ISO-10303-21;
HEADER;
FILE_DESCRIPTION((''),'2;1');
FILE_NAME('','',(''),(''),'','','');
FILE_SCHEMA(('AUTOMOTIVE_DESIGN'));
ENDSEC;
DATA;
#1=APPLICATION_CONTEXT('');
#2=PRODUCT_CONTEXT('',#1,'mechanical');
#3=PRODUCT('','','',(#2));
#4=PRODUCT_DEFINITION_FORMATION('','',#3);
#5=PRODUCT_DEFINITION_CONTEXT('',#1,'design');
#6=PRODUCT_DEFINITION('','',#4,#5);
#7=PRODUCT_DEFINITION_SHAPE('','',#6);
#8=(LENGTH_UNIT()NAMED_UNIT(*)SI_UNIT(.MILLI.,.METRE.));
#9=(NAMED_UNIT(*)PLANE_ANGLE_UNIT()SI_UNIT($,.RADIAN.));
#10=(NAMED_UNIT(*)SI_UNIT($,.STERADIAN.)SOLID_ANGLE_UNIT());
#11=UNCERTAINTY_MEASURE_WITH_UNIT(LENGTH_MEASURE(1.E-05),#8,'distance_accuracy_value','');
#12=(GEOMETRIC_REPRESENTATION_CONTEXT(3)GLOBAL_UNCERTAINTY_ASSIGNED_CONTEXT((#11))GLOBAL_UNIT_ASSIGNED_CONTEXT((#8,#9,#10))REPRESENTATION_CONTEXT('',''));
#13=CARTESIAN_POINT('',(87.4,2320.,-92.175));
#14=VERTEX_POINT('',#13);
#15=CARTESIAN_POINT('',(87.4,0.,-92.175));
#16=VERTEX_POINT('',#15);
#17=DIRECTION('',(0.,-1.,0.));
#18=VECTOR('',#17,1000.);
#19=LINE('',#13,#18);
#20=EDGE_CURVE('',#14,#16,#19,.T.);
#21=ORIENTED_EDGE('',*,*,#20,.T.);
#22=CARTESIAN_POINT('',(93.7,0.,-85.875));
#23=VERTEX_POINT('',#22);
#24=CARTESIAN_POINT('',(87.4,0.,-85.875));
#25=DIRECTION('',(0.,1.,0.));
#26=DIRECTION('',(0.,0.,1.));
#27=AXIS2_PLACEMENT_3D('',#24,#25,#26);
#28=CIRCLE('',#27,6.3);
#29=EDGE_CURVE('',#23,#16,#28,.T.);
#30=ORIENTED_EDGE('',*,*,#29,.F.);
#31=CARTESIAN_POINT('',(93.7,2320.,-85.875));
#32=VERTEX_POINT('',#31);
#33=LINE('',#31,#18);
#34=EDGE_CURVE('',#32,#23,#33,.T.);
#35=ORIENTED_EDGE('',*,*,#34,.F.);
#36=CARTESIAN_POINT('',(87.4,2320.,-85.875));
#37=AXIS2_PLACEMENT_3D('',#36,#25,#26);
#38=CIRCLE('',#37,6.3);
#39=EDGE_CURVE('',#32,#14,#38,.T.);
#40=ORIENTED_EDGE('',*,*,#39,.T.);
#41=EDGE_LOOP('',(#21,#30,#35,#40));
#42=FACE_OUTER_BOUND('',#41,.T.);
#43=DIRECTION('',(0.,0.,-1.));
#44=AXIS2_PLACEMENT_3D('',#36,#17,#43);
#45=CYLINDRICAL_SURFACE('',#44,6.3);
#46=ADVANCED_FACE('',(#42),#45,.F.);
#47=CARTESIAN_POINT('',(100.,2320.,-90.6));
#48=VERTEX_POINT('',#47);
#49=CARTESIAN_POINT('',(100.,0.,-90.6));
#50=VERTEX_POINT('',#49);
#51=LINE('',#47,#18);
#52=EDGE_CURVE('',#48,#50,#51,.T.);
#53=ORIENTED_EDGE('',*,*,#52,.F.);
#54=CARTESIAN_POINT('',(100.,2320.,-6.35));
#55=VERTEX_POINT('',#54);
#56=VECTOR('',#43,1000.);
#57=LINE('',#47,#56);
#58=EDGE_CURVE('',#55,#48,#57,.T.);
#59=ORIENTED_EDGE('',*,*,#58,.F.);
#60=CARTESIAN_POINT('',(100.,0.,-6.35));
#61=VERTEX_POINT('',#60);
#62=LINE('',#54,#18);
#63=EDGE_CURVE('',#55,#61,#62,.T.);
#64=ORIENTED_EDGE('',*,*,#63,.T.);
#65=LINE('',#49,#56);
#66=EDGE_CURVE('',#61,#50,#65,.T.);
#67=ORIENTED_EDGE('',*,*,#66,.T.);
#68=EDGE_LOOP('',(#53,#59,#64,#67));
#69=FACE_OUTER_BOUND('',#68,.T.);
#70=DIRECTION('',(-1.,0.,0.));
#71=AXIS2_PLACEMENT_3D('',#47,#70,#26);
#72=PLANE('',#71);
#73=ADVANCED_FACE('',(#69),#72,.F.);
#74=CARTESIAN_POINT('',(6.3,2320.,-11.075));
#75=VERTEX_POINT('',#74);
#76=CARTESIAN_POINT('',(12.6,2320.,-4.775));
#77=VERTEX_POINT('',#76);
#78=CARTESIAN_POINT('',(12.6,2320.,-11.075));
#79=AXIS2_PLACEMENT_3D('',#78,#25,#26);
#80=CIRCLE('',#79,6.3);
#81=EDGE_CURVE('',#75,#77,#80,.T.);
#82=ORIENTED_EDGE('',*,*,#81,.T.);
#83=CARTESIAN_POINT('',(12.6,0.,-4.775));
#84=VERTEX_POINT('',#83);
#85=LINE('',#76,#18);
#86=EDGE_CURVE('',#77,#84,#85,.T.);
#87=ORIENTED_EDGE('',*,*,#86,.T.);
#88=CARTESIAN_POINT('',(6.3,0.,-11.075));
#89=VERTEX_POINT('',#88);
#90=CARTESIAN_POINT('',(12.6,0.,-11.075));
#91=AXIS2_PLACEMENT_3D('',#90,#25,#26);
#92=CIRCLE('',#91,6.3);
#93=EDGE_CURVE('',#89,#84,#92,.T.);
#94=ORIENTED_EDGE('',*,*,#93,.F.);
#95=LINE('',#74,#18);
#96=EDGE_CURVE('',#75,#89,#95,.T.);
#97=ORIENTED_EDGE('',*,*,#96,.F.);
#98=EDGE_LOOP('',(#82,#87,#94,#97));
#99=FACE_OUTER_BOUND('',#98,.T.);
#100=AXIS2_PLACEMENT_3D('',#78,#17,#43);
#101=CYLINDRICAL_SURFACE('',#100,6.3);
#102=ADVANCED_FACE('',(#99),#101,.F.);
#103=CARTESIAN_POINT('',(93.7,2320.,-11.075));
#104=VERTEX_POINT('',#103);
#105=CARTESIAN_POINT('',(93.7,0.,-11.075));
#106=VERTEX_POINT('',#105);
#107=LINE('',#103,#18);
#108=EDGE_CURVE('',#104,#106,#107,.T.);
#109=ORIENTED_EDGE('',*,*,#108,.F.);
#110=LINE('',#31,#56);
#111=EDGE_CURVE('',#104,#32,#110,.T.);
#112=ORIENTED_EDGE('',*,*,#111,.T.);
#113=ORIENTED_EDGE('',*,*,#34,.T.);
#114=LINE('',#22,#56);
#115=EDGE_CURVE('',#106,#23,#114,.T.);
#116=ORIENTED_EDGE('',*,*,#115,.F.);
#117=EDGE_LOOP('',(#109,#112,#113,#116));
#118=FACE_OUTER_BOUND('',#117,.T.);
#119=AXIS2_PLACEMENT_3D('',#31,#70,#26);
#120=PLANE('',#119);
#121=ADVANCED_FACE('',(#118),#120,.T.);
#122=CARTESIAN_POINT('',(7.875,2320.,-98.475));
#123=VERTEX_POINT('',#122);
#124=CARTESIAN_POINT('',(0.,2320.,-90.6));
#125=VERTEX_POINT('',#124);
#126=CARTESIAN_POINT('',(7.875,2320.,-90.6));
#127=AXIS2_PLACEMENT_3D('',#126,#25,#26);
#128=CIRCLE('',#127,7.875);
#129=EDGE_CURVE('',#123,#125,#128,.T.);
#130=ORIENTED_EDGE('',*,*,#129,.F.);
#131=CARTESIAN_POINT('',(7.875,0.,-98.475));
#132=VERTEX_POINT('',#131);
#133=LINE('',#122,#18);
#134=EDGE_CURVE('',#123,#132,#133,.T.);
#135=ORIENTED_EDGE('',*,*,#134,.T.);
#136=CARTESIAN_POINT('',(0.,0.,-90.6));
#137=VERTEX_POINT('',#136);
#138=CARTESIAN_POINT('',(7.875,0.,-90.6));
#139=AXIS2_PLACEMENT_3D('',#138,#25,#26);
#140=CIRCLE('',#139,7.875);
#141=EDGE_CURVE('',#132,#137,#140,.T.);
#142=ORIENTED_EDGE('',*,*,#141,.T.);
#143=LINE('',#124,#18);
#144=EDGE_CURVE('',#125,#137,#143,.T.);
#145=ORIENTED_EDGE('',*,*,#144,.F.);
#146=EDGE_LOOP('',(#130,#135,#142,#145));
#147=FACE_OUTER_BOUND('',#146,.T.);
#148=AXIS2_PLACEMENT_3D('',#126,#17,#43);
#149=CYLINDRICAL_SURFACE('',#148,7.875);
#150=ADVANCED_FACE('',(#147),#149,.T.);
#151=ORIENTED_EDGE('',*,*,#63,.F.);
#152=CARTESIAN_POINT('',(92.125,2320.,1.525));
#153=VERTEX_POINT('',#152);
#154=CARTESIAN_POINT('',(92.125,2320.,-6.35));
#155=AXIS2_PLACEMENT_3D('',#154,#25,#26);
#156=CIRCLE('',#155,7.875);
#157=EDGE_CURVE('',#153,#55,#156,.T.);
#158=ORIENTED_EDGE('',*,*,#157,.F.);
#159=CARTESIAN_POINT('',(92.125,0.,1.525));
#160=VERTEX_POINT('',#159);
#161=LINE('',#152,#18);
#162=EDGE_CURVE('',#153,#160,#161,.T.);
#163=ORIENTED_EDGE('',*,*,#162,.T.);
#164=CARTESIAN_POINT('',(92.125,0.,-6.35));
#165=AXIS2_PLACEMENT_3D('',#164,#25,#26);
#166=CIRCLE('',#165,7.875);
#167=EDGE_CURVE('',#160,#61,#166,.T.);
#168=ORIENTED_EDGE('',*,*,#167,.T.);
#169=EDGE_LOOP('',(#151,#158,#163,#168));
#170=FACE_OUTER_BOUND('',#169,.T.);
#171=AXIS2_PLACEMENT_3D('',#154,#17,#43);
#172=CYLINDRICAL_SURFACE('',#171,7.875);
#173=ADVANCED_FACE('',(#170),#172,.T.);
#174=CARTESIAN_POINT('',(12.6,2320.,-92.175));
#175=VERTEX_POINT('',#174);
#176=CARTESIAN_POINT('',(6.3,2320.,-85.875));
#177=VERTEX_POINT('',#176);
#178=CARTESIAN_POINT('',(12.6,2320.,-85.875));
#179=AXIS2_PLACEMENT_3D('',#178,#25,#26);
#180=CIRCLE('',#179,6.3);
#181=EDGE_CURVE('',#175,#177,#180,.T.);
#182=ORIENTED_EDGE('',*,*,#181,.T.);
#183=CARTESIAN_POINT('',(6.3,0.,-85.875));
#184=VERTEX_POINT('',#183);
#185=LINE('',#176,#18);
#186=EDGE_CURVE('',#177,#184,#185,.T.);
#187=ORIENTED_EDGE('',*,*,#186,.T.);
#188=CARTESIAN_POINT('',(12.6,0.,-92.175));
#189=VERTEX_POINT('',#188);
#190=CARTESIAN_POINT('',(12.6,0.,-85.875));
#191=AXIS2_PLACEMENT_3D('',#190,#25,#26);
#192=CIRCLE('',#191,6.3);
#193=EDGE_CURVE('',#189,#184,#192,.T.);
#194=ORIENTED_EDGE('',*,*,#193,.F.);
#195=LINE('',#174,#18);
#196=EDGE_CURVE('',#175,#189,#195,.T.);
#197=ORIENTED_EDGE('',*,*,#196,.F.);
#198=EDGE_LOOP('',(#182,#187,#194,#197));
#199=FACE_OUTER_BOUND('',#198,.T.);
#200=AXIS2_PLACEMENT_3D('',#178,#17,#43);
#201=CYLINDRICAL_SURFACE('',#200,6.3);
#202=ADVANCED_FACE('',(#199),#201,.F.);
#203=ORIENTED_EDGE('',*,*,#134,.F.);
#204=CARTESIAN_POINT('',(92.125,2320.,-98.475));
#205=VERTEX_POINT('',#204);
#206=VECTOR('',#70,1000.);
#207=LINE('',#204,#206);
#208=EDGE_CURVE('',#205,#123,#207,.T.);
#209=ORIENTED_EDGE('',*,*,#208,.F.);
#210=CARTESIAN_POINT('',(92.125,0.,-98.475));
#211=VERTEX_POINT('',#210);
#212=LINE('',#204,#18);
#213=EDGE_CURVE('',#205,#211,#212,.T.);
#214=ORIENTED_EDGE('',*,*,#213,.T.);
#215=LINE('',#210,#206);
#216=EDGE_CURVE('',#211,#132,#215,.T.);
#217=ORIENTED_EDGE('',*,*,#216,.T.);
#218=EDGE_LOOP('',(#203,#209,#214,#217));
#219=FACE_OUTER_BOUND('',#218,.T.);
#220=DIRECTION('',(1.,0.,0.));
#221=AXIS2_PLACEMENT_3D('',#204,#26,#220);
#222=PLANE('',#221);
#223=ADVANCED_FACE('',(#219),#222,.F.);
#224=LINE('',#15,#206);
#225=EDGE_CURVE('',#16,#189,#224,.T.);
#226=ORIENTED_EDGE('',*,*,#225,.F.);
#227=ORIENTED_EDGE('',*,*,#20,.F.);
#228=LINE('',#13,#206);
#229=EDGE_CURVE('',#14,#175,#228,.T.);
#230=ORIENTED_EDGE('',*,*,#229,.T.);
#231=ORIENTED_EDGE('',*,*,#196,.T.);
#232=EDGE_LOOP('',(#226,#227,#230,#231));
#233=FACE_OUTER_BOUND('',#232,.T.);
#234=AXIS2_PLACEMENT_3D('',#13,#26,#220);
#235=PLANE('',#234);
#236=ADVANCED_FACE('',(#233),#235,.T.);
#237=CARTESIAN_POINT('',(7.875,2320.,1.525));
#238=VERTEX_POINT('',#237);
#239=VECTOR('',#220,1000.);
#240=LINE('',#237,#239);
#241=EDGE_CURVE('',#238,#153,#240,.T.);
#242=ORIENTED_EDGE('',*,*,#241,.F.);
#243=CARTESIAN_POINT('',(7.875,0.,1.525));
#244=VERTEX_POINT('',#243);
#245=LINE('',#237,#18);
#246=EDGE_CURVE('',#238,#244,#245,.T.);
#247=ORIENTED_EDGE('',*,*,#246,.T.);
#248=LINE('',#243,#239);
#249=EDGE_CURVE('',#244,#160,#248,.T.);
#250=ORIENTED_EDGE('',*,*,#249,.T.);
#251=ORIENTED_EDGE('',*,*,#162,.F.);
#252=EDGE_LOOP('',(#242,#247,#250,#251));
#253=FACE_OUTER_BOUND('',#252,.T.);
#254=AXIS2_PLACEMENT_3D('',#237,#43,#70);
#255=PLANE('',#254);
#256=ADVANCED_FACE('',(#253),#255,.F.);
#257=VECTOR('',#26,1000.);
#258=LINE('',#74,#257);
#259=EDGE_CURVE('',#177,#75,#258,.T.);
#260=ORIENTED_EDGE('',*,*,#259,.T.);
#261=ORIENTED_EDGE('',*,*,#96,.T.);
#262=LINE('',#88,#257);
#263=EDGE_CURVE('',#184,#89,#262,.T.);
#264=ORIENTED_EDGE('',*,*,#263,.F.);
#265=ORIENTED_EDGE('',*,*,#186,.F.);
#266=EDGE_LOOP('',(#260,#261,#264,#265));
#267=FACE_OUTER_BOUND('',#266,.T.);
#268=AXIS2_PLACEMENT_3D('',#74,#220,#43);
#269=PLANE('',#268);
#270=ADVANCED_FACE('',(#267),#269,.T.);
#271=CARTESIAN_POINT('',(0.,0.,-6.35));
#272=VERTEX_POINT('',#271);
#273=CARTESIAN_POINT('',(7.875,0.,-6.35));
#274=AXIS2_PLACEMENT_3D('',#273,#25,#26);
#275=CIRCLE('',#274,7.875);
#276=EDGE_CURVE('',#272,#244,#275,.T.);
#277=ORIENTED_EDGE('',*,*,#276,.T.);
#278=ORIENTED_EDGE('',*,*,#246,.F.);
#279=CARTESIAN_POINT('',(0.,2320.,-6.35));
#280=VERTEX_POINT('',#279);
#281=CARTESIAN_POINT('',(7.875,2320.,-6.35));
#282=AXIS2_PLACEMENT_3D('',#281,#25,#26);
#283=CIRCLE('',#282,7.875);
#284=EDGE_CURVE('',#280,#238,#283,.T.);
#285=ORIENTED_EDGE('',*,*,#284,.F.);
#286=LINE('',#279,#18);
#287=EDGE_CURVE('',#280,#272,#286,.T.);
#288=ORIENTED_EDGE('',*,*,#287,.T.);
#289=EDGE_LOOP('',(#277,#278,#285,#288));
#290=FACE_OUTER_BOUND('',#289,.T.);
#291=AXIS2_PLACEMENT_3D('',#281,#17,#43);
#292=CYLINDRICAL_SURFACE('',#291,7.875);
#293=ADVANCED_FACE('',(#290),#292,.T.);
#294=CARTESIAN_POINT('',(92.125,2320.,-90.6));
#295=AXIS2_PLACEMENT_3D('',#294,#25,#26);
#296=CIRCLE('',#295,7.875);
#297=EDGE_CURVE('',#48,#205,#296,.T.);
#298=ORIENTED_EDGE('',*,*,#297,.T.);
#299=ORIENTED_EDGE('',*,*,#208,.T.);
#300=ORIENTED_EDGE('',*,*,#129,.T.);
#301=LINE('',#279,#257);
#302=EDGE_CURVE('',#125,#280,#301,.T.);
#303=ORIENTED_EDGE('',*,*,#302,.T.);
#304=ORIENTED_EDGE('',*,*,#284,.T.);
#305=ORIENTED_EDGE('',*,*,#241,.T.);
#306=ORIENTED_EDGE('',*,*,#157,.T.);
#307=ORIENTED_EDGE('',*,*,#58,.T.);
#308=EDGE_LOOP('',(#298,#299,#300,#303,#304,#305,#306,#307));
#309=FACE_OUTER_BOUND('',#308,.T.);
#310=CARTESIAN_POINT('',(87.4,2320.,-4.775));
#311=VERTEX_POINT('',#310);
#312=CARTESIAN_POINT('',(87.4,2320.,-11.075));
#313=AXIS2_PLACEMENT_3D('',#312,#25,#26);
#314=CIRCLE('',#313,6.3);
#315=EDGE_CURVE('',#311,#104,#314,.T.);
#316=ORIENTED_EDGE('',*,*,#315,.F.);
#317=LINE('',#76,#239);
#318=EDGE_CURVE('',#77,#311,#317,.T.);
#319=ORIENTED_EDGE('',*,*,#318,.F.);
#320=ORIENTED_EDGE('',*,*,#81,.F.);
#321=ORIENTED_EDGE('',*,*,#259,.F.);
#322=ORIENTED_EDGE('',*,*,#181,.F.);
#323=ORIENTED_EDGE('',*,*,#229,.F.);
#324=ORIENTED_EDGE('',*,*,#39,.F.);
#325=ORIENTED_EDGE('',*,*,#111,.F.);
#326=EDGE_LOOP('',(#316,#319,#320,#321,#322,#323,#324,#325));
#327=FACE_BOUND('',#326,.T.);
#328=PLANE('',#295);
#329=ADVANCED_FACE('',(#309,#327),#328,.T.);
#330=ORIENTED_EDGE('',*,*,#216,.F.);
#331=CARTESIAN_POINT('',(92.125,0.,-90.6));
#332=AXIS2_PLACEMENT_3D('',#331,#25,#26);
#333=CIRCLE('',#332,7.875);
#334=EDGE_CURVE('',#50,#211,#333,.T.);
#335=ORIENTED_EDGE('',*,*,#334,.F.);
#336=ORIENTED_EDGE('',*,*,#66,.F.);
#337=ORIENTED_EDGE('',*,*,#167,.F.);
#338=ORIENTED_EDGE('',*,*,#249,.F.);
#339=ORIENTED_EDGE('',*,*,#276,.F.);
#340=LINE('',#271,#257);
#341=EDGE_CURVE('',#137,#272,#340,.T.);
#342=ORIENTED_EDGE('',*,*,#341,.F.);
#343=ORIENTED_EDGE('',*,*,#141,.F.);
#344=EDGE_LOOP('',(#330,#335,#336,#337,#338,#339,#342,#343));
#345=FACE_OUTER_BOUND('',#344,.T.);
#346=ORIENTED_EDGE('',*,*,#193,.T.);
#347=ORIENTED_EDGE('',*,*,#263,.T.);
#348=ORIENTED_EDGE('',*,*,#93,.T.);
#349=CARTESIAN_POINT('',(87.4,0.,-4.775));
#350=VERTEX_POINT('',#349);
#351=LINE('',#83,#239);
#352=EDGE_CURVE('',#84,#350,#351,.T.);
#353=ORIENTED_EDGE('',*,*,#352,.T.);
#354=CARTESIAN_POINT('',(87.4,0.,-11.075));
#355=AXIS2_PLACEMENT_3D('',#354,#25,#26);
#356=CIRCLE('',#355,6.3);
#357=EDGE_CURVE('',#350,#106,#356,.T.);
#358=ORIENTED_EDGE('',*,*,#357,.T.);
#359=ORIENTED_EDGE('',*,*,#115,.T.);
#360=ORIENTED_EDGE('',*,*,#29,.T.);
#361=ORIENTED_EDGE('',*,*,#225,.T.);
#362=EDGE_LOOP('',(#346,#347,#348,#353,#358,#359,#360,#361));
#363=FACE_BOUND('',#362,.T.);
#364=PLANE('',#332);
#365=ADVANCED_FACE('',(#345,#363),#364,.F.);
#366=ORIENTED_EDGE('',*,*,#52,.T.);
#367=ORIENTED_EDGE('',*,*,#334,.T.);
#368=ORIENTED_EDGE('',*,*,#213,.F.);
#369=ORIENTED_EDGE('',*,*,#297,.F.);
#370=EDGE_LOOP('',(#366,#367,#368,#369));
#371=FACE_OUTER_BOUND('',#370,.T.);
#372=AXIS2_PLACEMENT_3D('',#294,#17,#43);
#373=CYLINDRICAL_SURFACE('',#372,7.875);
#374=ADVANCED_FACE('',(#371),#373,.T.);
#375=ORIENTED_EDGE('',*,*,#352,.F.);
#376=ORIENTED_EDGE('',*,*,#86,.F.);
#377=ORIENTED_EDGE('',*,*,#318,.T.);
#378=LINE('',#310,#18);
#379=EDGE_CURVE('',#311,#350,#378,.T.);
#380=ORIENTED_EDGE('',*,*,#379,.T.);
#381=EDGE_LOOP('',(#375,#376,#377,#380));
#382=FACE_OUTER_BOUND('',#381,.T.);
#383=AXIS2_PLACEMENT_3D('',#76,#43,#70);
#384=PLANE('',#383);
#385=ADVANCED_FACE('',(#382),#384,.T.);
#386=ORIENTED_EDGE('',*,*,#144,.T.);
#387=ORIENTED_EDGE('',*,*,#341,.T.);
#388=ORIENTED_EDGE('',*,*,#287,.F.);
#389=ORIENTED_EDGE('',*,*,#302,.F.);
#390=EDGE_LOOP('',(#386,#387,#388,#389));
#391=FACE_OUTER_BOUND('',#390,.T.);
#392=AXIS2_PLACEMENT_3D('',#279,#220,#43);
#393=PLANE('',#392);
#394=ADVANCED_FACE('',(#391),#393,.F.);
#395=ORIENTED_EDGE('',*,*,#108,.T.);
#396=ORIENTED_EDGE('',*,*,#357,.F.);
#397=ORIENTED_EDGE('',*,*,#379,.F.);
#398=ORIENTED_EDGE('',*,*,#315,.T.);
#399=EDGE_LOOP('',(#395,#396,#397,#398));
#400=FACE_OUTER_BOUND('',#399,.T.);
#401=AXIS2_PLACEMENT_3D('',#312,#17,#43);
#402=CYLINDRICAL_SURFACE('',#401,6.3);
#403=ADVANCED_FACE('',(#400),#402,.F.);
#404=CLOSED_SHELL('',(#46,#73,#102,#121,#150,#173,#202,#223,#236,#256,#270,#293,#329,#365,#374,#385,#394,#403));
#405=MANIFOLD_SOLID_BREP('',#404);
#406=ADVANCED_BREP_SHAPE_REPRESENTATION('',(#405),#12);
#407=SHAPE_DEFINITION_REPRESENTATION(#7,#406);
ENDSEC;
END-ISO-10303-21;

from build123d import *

# Parameters (mm, degrees)
BOSS_EXTRUDE1_DEPTH = 2320


with BuildPart() as part:
    # Sketch2 → Boss-Extrude1 (new body)
    with BuildSketch(Plane(origin=(0, 0, 0), x_dir=(1, 0, 0), z_dir=(0, 1, 0))):
        with BuildLine():
            Line((7.875, -1.525), (92.125, -1.525))
            ThreePointArc((92.125, -1.525), (97.693465902, 0.781534098), (100, 6.35))
            Line((100, 6.35), (100, 90.6))
            ThreePointArc((100, 90.6), (97.693465902, 96.168465902), (92.125, 98.475))
            Line((92.125, 98.475), (7.875, 98.475))
            ThreePointArc((7.875, 98.475), (2.306534098, 96.168465902), (0, 90.6))
            Line((0, 90.6), (0, 6.35))
            ThreePointArc((0, 6.35), (2.306534098, 0.781534098), (7.875, -1.525))
        make_face()
        with BuildLine():
            Line((12.6, 4.775), (87.4, 4.775))
            ThreePointArc((87.4, 4.775), (91.854772721, 6.620227279), (93.7, 11.075))
            Line((93.7, 11.075), (93.7, 85.875))
            ThreePointArc((93.7, 85.875), (91.854772721, 90.329772721), (87.4, 92.175))
            Line((87.4, 92.175), (12.6, 92.175))
            ThreePointArc((12.6, 92.175), (8.145227279, 90.329772721), (6.3, 85.875))
            Line((6.3, 85.875), (6.3, 11.075))
            ThreePointArc((6.3, 11.075), (8.145227279, 6.620227279), (12.6, 4.775))
        make_face(mode=Mode.SUBTRACT)
    extrude(amount=BOSS_EXTRUDE1_DEPTH)


solid = part.part
